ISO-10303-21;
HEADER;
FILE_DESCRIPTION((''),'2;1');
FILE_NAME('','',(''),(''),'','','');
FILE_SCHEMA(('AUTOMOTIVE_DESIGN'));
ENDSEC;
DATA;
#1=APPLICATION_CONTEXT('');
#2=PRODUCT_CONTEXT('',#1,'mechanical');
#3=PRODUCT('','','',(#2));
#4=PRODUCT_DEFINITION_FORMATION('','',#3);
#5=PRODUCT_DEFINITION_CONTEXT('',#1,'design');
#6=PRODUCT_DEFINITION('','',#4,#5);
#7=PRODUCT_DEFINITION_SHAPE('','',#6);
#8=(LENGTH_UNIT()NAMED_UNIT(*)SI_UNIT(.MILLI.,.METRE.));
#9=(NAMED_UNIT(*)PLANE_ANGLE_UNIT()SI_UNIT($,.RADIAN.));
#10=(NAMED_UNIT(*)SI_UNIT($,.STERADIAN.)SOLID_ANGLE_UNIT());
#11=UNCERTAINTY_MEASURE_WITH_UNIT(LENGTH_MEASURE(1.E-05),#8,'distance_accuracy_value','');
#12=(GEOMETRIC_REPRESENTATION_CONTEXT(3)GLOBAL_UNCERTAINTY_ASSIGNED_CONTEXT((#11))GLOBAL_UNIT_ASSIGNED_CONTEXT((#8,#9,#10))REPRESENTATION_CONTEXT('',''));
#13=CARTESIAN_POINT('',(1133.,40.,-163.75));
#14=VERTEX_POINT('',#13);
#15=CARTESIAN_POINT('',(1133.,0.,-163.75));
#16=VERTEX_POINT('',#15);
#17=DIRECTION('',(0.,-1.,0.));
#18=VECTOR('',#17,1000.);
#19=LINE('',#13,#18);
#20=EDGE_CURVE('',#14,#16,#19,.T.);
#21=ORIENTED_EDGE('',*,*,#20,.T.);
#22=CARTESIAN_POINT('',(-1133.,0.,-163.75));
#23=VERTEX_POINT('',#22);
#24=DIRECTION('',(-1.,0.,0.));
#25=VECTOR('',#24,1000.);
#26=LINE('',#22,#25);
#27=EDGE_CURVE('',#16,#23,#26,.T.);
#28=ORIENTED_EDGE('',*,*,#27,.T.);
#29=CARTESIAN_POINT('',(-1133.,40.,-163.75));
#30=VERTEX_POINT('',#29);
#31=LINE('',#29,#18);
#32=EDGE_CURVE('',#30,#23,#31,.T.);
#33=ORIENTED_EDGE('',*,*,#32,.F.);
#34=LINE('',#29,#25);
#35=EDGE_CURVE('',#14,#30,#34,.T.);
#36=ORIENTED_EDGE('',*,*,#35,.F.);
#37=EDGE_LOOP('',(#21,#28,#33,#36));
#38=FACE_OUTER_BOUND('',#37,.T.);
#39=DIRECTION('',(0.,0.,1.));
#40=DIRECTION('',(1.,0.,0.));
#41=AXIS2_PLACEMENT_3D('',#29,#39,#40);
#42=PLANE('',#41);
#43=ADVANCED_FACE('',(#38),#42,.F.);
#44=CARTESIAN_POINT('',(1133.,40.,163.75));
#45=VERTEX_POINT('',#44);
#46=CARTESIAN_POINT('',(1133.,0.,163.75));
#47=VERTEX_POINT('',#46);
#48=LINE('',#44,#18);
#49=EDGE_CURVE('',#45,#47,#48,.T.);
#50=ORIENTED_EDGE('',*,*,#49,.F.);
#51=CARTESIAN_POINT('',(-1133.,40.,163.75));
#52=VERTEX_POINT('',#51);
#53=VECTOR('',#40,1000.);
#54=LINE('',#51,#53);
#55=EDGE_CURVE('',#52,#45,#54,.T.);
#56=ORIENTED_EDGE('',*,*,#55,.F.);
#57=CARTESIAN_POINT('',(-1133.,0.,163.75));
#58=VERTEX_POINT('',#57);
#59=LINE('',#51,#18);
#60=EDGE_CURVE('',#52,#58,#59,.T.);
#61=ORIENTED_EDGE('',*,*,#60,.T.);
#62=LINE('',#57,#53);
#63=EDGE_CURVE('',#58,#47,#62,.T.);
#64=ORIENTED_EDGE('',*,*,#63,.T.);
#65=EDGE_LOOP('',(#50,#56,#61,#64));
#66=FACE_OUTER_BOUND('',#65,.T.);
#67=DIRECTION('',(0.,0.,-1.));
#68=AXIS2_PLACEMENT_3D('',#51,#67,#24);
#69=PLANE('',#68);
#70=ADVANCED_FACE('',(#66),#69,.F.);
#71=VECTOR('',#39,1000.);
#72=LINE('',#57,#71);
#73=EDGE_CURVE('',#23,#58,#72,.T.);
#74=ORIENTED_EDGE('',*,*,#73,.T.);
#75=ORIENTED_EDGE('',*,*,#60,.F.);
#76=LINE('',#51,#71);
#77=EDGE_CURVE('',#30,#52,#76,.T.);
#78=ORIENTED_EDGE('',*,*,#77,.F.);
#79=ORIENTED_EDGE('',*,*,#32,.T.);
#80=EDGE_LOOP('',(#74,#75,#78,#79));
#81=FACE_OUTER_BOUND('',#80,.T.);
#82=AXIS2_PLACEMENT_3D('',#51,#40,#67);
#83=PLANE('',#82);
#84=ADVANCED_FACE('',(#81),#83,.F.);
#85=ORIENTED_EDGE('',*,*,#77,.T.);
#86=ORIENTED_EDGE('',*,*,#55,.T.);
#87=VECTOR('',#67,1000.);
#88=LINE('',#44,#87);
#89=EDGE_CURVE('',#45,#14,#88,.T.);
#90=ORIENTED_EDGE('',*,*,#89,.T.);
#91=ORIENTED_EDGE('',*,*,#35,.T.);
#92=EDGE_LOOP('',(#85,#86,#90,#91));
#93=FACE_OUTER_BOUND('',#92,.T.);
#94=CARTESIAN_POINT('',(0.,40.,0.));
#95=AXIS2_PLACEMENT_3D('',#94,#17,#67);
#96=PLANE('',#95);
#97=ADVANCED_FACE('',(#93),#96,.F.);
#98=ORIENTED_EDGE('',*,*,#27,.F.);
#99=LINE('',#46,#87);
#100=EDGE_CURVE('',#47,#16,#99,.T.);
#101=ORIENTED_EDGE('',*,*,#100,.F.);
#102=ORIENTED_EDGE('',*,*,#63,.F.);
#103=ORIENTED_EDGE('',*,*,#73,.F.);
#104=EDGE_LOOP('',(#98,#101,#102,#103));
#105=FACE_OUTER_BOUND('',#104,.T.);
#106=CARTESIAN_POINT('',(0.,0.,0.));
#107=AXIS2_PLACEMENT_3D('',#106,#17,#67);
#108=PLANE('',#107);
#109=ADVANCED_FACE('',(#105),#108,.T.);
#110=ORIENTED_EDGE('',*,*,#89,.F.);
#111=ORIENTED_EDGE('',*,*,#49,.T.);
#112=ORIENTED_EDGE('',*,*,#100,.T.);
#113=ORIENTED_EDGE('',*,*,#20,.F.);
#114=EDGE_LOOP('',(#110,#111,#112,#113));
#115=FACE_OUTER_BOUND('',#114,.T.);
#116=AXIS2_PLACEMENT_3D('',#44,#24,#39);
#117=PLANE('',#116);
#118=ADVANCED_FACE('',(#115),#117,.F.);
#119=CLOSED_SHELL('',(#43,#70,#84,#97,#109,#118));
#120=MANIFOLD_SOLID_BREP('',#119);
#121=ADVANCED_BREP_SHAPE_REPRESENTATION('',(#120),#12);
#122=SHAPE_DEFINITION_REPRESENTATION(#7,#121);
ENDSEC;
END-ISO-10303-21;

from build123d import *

# Parameters (mm, degrees)
SKETCH_1_W      = 2266
SKETCH_1_H      = 327.5
EXTRUDE_1_DEPTH = 40


with BuildPart() as part:
    # 草图1 → 凸台-拉伸1 (new body)
    with BuildSketch(Plane(origin=(0, 0, 0), x_dir=(1, 0, 0), z_dir=(0, 1, 0))):
        Rectangle(SKETCH_1_W, SKETCH_1_H)
    extrude(amount=EXTRUDE_1_DEPTH)


solid = part.part
